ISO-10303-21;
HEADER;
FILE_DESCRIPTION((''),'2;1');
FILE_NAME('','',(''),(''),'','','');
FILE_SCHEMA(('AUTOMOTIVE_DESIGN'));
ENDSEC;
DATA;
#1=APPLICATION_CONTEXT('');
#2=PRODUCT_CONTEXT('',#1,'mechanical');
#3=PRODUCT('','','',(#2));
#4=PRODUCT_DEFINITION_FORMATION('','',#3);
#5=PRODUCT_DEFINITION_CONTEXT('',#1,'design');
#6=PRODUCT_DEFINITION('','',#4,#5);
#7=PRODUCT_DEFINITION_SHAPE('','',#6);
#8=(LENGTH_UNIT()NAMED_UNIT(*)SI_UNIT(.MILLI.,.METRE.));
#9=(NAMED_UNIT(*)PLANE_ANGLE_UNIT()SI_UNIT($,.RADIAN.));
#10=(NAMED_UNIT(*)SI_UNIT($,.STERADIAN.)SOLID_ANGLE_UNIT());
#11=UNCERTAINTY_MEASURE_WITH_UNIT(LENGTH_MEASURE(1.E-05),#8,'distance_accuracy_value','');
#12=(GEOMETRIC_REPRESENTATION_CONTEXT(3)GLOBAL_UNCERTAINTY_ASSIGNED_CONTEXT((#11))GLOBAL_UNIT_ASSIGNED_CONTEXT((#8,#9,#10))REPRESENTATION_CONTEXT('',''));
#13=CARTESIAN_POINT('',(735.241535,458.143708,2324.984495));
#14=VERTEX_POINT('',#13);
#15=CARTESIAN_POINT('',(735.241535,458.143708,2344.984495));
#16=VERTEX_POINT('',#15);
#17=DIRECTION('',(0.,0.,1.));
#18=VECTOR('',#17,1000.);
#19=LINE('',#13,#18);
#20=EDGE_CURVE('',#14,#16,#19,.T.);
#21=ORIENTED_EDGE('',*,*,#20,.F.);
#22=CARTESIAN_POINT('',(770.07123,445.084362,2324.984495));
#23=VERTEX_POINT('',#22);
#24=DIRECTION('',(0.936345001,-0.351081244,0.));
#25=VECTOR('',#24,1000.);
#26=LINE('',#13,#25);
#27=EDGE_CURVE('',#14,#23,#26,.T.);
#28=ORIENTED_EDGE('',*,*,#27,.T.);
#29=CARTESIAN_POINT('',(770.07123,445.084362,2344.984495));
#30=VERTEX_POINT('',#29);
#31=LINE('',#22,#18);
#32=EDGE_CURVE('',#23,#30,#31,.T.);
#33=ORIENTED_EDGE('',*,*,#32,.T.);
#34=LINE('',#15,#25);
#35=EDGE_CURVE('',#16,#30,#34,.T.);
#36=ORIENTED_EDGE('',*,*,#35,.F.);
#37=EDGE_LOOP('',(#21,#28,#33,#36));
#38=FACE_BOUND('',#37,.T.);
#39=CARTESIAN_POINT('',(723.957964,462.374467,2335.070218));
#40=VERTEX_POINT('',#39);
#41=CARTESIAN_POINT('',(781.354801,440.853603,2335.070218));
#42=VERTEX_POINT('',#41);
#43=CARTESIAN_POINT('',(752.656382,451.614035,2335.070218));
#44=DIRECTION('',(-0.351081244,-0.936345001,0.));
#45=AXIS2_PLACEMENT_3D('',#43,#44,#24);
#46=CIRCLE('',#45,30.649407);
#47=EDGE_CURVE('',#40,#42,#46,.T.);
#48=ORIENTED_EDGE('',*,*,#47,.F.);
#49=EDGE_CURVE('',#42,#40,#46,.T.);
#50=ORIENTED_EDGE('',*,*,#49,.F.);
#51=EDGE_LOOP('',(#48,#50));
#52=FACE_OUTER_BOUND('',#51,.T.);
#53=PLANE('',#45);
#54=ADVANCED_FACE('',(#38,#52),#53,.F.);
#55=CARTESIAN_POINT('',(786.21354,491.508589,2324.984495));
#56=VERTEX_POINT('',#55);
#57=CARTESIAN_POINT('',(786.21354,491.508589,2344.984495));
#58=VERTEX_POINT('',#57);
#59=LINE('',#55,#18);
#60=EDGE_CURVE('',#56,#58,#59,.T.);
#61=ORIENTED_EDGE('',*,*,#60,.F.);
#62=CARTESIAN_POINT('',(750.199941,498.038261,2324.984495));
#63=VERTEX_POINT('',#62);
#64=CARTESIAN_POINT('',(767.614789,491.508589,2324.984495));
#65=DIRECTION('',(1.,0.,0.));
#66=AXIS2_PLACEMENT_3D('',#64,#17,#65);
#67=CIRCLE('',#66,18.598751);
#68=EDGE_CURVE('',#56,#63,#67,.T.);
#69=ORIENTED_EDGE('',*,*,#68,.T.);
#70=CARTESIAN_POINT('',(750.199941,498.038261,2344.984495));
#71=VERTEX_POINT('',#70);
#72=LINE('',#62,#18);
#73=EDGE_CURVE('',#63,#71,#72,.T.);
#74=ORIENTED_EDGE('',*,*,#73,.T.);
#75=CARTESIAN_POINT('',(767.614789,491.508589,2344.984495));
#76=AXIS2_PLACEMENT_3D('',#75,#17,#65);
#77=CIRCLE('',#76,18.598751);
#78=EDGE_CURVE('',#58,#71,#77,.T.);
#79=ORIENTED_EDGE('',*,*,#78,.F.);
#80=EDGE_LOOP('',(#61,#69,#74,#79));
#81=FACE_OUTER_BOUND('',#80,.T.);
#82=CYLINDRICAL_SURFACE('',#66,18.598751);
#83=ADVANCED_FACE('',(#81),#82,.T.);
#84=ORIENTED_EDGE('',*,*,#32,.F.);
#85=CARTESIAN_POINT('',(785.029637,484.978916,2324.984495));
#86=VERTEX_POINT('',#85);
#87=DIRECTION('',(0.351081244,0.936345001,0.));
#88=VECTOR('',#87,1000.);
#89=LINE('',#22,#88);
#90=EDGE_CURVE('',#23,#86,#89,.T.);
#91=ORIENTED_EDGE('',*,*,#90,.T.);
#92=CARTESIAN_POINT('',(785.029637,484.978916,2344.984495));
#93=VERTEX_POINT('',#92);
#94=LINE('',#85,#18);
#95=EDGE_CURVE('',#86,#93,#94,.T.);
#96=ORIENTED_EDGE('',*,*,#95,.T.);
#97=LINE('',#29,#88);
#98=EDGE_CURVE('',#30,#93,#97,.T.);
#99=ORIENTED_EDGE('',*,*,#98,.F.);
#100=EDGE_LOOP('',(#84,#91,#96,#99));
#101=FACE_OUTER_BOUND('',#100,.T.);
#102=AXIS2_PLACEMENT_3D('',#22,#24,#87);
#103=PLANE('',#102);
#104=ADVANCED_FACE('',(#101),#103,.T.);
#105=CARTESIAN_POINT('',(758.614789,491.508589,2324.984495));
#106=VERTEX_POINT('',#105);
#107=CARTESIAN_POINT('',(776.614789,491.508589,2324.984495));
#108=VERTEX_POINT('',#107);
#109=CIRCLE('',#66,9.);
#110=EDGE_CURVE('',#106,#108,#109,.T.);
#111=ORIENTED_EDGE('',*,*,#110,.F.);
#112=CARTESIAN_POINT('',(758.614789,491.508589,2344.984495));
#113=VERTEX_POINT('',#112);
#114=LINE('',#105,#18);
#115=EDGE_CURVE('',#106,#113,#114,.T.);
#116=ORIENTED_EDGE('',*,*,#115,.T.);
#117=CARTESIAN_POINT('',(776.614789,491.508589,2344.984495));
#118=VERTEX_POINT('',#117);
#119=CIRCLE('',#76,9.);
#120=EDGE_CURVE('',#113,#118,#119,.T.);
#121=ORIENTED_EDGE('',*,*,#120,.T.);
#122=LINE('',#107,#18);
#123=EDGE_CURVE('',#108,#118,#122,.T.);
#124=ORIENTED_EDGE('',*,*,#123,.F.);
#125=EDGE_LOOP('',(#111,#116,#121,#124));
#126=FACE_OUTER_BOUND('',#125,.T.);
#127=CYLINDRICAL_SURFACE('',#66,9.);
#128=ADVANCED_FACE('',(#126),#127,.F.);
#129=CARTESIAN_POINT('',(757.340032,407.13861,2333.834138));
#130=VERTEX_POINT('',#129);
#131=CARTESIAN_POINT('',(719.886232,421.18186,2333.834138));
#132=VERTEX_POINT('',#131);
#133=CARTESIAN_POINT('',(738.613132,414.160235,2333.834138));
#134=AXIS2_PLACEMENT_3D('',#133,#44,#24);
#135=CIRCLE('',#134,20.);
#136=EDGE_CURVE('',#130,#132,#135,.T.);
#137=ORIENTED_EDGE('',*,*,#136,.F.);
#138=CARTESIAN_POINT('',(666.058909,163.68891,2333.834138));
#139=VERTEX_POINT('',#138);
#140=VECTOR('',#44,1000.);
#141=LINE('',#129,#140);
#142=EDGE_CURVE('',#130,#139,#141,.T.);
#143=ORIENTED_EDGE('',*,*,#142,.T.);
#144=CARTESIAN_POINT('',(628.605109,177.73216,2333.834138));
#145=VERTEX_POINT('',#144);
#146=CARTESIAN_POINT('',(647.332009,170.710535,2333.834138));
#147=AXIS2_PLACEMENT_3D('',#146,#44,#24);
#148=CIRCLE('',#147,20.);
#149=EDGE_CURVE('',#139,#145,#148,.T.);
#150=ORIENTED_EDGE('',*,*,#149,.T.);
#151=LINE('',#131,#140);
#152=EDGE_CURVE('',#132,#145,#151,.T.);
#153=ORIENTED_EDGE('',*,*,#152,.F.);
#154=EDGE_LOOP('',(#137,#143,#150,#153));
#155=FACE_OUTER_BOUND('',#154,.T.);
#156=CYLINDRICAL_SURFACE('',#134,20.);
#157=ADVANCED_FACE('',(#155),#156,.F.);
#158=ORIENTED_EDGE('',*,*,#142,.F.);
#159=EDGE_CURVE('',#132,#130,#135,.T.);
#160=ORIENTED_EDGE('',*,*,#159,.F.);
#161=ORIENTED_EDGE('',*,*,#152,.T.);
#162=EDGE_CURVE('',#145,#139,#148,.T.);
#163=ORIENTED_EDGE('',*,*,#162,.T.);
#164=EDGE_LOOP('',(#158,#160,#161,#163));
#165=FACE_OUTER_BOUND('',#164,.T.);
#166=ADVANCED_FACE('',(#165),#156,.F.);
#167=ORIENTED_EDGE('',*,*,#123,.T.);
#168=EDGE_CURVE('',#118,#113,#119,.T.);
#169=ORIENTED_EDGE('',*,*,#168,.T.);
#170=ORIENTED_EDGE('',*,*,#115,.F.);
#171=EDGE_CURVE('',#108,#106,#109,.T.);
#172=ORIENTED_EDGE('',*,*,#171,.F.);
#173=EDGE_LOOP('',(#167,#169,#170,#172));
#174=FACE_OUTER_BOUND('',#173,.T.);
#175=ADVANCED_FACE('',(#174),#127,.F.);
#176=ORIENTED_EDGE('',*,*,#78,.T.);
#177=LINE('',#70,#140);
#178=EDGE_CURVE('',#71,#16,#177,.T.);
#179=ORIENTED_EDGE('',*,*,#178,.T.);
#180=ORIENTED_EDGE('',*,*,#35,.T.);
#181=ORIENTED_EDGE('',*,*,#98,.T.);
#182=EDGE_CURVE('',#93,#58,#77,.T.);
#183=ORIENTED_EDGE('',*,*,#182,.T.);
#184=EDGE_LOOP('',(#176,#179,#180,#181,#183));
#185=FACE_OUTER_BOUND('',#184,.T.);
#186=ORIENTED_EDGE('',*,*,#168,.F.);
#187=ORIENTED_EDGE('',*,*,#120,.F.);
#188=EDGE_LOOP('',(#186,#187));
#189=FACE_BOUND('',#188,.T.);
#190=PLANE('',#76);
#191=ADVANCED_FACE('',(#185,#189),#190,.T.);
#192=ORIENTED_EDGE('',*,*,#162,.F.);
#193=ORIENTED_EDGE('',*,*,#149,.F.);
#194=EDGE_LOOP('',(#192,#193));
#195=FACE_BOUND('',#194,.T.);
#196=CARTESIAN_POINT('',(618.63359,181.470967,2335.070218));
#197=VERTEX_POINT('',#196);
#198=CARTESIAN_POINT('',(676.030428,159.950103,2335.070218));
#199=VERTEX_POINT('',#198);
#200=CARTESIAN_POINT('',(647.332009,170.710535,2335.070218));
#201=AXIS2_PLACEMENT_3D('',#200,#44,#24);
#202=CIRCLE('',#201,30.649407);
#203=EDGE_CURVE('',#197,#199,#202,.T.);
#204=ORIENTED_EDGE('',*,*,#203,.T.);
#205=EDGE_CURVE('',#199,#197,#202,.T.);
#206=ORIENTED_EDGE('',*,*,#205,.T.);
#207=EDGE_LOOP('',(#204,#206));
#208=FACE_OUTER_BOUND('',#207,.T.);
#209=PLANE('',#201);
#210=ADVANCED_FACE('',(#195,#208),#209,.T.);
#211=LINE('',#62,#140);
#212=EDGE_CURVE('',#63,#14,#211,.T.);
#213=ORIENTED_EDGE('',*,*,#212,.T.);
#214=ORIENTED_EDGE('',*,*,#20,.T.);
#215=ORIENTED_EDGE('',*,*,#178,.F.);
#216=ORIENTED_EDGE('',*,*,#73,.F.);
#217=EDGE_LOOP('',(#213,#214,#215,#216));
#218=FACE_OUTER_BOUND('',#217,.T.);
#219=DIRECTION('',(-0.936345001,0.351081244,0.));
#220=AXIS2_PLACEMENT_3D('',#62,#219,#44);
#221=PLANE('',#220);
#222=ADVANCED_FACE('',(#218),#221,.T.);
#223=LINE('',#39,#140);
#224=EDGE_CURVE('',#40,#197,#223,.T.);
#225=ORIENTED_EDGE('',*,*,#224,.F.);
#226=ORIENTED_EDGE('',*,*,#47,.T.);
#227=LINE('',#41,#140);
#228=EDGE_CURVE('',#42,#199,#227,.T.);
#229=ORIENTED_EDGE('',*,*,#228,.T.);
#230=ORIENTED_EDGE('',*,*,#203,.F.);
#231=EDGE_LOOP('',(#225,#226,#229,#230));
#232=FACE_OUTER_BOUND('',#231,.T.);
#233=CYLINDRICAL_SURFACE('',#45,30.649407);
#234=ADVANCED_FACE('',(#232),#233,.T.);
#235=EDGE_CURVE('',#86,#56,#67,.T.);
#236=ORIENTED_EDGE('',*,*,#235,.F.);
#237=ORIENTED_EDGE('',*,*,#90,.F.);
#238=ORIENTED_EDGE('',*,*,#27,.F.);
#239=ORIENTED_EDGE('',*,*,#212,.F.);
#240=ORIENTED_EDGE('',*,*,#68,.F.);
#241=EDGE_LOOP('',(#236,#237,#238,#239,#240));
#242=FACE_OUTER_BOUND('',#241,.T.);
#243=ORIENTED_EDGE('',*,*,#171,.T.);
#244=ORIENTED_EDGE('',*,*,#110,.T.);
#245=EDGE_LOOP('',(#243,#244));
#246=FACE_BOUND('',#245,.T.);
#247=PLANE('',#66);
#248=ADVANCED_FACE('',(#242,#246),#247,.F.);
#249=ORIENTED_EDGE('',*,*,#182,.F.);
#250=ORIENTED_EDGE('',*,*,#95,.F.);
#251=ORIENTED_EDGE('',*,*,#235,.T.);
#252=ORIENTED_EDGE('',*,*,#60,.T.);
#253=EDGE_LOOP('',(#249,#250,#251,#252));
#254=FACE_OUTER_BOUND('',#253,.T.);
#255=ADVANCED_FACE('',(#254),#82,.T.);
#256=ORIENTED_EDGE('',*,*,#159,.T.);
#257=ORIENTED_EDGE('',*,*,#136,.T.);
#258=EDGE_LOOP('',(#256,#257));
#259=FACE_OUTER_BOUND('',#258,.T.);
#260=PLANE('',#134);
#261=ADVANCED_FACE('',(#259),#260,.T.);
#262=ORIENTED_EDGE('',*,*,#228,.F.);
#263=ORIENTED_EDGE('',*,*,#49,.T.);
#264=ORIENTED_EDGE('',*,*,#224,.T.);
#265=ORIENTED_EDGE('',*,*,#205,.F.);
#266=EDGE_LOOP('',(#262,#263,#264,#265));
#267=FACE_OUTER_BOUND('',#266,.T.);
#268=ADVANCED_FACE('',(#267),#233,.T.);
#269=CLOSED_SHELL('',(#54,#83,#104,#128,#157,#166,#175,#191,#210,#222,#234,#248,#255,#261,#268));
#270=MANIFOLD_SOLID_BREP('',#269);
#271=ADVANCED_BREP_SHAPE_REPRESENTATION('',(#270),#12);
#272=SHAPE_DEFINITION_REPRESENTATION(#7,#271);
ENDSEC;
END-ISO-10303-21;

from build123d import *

# Parameters (mm, degrees)
BOSS_EXTRUDE1_DEPTH = 300
BOSS_EXTRUDE2_DEPTH = 20
SKETCH3_R           = 20
CUT_EXTRUDE1_DEPTH  = 260


with BuildPart() as part:
    # Sketch1 → Boss-Extrude1 (new body)
    with BuildSketch(Plane(origin=(135.907089576, 362.468590855, 0), x_dir=(0.9363450005078556, -0.35108124419277087, 0), z_dir=(-0.35108124419277087, -0.9363450005078556, 0))):
        with BuildLine():
            ThreePointArc((546.192823225, 2365.719625064), (515.543416647, 2335.070218486), (546.192823225, 2304.420811908))
            ThreePointArc((546.192823225, 2304.420811908), (576.842229803, 2335.070218486), (546.192823225, 2365.719625064))
        make_face()
    extrude(amount=-BOSS_EXTRUDE1_DEPTH)

    # Sketch2 → Boss-Extrude2 (add)
    with BuildSketch(Plane.XY.offset(2344.984494649)):
        with BuildLine():
            Line((750.199941467, 498.038261237), (735.241534602, 458.143707723))
            Line((735.241534602, 458.143707723), (770.071229746, 445.084362397))
            Line((770.071229746, 445.084362397), (785.029636612, 484.978915911))
            ThreePointArc((785.029636612, 484.978915911), (774.144461703, 508.923436146), (750.199941467, 498.038261237))
        make_face()
        with BuildLine():
            ThreePointArc((760.635963738, 485.825631826), (773.297745788, 484.529763272), (774.593614342, 497.191545322))
            ThreePointArc((774.593614342, 497.191545322), (761.931832291, 498.487413876), (760.635963738, 485.825631826))
        make_face(mode=Mode.SUBTRACT)
    extrude(amount=-BOSS_EXTRUDE2_DEPTH)

    # Sketch3 → Cut-Extrude1 (cut)
    with BuildSketch(Plane(origin=(135.907089576, 362.468590855, 0), x_dir=(0.9363450005078556, -0.351081244192771, 0), z_dir=(-0.351081244192771, -0.9363450005078556, 0))):
        with Locations((546.192823225, 2333.834137652)):
            Circle(SKETCH3_R)
    extrude(amount=-CUT_EXTRUDE1_DEPTH, mode=Mode.SUBTRACT)


solid = part.part
